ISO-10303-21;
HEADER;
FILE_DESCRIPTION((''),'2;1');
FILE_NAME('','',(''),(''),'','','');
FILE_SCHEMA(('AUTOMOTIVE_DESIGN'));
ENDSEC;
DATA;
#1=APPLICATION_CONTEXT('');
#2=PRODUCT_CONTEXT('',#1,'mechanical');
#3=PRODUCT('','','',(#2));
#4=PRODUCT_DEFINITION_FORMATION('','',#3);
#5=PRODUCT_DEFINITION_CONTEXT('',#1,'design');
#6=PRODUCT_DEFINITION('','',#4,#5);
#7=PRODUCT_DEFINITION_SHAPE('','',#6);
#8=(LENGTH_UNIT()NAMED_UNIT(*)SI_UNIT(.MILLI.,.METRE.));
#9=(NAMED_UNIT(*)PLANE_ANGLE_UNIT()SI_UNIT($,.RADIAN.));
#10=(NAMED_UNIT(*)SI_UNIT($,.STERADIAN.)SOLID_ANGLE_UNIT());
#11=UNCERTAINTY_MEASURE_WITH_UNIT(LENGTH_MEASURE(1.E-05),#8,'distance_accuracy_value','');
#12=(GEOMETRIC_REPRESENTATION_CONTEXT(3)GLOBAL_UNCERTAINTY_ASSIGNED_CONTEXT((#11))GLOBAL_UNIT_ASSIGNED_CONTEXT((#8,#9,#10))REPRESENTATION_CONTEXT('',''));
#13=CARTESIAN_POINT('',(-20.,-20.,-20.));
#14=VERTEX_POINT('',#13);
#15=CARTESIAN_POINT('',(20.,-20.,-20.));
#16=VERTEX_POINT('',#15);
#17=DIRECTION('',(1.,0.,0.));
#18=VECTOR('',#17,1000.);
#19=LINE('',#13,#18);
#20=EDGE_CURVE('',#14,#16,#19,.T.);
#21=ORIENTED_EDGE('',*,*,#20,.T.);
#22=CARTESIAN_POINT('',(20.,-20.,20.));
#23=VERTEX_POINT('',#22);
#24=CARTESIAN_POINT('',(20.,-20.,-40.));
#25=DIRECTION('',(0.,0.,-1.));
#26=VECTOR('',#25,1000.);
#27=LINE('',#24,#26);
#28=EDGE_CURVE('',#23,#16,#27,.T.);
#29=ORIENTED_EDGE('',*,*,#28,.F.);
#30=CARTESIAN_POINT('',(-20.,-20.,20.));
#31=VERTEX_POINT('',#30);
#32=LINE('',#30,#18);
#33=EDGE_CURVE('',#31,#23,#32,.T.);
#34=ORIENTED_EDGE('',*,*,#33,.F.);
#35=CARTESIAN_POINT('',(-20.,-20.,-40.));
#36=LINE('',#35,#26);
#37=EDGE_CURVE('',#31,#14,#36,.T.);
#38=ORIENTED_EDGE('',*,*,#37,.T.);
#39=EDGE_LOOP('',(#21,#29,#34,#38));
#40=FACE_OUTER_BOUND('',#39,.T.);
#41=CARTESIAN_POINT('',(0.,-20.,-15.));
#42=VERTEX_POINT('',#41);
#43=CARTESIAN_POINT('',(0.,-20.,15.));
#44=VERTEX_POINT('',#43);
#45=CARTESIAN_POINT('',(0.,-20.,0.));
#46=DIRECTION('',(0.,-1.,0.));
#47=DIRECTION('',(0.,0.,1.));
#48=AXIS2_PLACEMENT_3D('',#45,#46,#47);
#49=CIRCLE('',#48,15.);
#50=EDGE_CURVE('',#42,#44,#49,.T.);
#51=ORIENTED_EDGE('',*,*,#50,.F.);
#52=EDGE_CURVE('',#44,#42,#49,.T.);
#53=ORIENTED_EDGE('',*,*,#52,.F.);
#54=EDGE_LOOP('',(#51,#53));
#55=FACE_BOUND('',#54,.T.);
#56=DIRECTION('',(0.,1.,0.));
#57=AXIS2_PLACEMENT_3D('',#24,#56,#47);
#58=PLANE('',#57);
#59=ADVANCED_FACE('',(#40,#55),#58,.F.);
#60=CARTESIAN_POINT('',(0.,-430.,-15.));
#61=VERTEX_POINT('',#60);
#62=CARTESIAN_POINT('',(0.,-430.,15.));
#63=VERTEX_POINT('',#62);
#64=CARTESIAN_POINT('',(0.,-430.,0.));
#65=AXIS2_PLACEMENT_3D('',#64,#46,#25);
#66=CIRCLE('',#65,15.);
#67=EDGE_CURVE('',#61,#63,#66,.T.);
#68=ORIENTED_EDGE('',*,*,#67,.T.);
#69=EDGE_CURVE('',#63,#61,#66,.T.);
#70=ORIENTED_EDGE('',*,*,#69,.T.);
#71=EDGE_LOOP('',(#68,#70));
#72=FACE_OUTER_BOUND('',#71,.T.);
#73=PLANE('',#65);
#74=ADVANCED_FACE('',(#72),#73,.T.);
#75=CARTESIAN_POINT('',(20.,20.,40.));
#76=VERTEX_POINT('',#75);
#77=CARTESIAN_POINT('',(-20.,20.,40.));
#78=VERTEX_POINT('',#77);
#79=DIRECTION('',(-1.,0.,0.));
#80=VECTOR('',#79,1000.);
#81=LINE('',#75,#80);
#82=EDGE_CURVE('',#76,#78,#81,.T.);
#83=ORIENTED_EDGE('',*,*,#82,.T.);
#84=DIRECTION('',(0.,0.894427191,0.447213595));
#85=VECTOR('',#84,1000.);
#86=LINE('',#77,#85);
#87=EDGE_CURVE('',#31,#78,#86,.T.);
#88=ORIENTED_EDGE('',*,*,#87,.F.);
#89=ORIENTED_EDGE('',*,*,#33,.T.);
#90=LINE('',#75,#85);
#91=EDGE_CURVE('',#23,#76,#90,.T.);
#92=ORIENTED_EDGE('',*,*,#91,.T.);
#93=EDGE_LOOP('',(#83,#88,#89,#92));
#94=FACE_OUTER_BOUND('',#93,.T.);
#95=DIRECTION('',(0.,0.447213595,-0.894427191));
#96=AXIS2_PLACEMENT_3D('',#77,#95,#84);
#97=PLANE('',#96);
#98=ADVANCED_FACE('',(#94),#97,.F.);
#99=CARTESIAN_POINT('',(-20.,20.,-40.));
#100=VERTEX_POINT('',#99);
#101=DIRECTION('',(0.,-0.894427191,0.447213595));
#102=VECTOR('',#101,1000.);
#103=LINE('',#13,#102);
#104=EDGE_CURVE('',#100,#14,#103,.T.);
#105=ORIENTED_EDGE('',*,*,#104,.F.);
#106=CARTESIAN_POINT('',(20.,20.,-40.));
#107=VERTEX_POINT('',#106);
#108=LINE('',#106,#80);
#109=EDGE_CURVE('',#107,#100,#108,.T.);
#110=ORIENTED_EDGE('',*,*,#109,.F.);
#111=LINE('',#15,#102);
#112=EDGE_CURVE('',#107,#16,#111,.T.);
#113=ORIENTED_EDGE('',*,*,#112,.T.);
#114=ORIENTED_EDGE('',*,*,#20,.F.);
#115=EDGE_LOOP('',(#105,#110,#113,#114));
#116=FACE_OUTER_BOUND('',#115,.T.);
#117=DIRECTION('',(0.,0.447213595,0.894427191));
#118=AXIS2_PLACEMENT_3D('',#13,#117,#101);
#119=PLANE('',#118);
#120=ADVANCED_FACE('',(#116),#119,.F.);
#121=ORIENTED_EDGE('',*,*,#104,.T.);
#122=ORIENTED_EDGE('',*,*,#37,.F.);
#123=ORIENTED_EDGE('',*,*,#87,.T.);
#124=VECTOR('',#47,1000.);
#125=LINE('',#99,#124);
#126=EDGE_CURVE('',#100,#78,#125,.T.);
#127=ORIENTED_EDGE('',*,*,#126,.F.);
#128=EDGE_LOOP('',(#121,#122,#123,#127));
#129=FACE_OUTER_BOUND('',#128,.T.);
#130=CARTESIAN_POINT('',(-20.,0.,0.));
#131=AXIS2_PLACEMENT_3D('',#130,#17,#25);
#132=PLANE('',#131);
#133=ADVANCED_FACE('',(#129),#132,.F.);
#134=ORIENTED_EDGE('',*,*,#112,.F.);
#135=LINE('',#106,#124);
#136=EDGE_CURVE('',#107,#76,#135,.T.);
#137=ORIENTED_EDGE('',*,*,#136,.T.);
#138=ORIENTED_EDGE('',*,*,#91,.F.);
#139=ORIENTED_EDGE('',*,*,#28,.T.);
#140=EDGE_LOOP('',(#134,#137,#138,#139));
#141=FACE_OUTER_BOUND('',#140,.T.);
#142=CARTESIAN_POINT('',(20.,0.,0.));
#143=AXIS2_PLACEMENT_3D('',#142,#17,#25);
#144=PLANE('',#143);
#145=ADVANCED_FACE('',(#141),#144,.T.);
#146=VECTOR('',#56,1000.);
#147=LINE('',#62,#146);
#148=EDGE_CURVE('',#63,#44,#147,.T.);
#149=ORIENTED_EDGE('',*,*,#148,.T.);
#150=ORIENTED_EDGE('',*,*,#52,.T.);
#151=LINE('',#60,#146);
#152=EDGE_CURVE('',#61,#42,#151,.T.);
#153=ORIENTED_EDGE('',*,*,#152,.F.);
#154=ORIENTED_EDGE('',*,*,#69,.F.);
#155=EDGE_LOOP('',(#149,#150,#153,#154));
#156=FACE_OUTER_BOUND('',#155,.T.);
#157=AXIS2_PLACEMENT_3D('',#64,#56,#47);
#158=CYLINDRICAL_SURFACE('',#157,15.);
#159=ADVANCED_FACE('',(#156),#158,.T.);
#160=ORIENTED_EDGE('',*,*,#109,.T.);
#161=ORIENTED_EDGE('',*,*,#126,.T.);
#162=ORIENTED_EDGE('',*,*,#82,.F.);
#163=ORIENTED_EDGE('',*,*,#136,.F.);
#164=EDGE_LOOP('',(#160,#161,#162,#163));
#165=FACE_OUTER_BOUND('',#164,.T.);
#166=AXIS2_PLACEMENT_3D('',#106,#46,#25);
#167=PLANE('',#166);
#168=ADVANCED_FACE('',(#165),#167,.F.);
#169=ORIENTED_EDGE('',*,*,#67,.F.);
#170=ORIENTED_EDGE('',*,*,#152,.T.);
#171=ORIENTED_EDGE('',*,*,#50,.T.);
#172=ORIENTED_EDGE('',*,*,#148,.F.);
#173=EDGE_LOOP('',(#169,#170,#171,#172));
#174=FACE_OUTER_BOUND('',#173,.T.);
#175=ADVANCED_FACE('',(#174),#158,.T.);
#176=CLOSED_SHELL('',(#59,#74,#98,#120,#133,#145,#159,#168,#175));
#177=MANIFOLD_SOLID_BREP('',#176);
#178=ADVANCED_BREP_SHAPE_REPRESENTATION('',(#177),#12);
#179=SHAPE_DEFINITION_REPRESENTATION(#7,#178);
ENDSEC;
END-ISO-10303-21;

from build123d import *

# Parameters (mm, degrees)
SKETCH1_W               = 80
SKETCH1_H               = 40
BOSS_EXTRUDE1_DEPTH     = 20
CUT_EXTRUDE1_DEPTH      = 49.989794856
CUT_EXTRUDE1_DEPTH_BACK = 49.989794856
SKETCH3_R               = 15
BOSS_EXTRUDE2_DEPTH     = 410


with BuildPart() as part:
    # Sketch1 → Boss-Extrude1 (new, symmetric)
    with BuildSketch(Plane(origin=(0, 0, 0), x_dir=(0, 0, -1), z_dir=(1, 0, 0))):
        Rectangle(SKETCH1_W, SKETCH1_H)
    extrude(amount=BOSS_EXTRUDE1_DEPTH, both=True)

    # Sketch2 → Cut-Extrude1 (cut, two sides: drawn at the far end of the back side and taken through both)
    with BuildSketch(Plane(origin=(0, 0, 0), x_dir=(0, 0, -1), z_dir=(1, 0, 0)).offset(-CUT_EXTRUDE1_DEPTH_BACK)):
        Polygon((-40, 20), (-20, -20), (-40, -20), align=None)
        Polygon((40, 20), (40, -20), (20, -20), align=None)
    extrude(amount=CUT_EXTRUDE1_DEPTH + CUT_EXTRUDE1_DEPTH_BACK, mode=Mode.SUBTRACT)

    # Sketch3 → Boss-Extrude2 (add)
    with BuildSketch(Plane.XZ.offset(20)):
        with Locations(Location((0, 0, 0), (0, 0, 90))):
            Circle(SKETCH3_R)
    extrude(amount=BOSS_EXTRUDE2_DEPTH)


solid = part.part
